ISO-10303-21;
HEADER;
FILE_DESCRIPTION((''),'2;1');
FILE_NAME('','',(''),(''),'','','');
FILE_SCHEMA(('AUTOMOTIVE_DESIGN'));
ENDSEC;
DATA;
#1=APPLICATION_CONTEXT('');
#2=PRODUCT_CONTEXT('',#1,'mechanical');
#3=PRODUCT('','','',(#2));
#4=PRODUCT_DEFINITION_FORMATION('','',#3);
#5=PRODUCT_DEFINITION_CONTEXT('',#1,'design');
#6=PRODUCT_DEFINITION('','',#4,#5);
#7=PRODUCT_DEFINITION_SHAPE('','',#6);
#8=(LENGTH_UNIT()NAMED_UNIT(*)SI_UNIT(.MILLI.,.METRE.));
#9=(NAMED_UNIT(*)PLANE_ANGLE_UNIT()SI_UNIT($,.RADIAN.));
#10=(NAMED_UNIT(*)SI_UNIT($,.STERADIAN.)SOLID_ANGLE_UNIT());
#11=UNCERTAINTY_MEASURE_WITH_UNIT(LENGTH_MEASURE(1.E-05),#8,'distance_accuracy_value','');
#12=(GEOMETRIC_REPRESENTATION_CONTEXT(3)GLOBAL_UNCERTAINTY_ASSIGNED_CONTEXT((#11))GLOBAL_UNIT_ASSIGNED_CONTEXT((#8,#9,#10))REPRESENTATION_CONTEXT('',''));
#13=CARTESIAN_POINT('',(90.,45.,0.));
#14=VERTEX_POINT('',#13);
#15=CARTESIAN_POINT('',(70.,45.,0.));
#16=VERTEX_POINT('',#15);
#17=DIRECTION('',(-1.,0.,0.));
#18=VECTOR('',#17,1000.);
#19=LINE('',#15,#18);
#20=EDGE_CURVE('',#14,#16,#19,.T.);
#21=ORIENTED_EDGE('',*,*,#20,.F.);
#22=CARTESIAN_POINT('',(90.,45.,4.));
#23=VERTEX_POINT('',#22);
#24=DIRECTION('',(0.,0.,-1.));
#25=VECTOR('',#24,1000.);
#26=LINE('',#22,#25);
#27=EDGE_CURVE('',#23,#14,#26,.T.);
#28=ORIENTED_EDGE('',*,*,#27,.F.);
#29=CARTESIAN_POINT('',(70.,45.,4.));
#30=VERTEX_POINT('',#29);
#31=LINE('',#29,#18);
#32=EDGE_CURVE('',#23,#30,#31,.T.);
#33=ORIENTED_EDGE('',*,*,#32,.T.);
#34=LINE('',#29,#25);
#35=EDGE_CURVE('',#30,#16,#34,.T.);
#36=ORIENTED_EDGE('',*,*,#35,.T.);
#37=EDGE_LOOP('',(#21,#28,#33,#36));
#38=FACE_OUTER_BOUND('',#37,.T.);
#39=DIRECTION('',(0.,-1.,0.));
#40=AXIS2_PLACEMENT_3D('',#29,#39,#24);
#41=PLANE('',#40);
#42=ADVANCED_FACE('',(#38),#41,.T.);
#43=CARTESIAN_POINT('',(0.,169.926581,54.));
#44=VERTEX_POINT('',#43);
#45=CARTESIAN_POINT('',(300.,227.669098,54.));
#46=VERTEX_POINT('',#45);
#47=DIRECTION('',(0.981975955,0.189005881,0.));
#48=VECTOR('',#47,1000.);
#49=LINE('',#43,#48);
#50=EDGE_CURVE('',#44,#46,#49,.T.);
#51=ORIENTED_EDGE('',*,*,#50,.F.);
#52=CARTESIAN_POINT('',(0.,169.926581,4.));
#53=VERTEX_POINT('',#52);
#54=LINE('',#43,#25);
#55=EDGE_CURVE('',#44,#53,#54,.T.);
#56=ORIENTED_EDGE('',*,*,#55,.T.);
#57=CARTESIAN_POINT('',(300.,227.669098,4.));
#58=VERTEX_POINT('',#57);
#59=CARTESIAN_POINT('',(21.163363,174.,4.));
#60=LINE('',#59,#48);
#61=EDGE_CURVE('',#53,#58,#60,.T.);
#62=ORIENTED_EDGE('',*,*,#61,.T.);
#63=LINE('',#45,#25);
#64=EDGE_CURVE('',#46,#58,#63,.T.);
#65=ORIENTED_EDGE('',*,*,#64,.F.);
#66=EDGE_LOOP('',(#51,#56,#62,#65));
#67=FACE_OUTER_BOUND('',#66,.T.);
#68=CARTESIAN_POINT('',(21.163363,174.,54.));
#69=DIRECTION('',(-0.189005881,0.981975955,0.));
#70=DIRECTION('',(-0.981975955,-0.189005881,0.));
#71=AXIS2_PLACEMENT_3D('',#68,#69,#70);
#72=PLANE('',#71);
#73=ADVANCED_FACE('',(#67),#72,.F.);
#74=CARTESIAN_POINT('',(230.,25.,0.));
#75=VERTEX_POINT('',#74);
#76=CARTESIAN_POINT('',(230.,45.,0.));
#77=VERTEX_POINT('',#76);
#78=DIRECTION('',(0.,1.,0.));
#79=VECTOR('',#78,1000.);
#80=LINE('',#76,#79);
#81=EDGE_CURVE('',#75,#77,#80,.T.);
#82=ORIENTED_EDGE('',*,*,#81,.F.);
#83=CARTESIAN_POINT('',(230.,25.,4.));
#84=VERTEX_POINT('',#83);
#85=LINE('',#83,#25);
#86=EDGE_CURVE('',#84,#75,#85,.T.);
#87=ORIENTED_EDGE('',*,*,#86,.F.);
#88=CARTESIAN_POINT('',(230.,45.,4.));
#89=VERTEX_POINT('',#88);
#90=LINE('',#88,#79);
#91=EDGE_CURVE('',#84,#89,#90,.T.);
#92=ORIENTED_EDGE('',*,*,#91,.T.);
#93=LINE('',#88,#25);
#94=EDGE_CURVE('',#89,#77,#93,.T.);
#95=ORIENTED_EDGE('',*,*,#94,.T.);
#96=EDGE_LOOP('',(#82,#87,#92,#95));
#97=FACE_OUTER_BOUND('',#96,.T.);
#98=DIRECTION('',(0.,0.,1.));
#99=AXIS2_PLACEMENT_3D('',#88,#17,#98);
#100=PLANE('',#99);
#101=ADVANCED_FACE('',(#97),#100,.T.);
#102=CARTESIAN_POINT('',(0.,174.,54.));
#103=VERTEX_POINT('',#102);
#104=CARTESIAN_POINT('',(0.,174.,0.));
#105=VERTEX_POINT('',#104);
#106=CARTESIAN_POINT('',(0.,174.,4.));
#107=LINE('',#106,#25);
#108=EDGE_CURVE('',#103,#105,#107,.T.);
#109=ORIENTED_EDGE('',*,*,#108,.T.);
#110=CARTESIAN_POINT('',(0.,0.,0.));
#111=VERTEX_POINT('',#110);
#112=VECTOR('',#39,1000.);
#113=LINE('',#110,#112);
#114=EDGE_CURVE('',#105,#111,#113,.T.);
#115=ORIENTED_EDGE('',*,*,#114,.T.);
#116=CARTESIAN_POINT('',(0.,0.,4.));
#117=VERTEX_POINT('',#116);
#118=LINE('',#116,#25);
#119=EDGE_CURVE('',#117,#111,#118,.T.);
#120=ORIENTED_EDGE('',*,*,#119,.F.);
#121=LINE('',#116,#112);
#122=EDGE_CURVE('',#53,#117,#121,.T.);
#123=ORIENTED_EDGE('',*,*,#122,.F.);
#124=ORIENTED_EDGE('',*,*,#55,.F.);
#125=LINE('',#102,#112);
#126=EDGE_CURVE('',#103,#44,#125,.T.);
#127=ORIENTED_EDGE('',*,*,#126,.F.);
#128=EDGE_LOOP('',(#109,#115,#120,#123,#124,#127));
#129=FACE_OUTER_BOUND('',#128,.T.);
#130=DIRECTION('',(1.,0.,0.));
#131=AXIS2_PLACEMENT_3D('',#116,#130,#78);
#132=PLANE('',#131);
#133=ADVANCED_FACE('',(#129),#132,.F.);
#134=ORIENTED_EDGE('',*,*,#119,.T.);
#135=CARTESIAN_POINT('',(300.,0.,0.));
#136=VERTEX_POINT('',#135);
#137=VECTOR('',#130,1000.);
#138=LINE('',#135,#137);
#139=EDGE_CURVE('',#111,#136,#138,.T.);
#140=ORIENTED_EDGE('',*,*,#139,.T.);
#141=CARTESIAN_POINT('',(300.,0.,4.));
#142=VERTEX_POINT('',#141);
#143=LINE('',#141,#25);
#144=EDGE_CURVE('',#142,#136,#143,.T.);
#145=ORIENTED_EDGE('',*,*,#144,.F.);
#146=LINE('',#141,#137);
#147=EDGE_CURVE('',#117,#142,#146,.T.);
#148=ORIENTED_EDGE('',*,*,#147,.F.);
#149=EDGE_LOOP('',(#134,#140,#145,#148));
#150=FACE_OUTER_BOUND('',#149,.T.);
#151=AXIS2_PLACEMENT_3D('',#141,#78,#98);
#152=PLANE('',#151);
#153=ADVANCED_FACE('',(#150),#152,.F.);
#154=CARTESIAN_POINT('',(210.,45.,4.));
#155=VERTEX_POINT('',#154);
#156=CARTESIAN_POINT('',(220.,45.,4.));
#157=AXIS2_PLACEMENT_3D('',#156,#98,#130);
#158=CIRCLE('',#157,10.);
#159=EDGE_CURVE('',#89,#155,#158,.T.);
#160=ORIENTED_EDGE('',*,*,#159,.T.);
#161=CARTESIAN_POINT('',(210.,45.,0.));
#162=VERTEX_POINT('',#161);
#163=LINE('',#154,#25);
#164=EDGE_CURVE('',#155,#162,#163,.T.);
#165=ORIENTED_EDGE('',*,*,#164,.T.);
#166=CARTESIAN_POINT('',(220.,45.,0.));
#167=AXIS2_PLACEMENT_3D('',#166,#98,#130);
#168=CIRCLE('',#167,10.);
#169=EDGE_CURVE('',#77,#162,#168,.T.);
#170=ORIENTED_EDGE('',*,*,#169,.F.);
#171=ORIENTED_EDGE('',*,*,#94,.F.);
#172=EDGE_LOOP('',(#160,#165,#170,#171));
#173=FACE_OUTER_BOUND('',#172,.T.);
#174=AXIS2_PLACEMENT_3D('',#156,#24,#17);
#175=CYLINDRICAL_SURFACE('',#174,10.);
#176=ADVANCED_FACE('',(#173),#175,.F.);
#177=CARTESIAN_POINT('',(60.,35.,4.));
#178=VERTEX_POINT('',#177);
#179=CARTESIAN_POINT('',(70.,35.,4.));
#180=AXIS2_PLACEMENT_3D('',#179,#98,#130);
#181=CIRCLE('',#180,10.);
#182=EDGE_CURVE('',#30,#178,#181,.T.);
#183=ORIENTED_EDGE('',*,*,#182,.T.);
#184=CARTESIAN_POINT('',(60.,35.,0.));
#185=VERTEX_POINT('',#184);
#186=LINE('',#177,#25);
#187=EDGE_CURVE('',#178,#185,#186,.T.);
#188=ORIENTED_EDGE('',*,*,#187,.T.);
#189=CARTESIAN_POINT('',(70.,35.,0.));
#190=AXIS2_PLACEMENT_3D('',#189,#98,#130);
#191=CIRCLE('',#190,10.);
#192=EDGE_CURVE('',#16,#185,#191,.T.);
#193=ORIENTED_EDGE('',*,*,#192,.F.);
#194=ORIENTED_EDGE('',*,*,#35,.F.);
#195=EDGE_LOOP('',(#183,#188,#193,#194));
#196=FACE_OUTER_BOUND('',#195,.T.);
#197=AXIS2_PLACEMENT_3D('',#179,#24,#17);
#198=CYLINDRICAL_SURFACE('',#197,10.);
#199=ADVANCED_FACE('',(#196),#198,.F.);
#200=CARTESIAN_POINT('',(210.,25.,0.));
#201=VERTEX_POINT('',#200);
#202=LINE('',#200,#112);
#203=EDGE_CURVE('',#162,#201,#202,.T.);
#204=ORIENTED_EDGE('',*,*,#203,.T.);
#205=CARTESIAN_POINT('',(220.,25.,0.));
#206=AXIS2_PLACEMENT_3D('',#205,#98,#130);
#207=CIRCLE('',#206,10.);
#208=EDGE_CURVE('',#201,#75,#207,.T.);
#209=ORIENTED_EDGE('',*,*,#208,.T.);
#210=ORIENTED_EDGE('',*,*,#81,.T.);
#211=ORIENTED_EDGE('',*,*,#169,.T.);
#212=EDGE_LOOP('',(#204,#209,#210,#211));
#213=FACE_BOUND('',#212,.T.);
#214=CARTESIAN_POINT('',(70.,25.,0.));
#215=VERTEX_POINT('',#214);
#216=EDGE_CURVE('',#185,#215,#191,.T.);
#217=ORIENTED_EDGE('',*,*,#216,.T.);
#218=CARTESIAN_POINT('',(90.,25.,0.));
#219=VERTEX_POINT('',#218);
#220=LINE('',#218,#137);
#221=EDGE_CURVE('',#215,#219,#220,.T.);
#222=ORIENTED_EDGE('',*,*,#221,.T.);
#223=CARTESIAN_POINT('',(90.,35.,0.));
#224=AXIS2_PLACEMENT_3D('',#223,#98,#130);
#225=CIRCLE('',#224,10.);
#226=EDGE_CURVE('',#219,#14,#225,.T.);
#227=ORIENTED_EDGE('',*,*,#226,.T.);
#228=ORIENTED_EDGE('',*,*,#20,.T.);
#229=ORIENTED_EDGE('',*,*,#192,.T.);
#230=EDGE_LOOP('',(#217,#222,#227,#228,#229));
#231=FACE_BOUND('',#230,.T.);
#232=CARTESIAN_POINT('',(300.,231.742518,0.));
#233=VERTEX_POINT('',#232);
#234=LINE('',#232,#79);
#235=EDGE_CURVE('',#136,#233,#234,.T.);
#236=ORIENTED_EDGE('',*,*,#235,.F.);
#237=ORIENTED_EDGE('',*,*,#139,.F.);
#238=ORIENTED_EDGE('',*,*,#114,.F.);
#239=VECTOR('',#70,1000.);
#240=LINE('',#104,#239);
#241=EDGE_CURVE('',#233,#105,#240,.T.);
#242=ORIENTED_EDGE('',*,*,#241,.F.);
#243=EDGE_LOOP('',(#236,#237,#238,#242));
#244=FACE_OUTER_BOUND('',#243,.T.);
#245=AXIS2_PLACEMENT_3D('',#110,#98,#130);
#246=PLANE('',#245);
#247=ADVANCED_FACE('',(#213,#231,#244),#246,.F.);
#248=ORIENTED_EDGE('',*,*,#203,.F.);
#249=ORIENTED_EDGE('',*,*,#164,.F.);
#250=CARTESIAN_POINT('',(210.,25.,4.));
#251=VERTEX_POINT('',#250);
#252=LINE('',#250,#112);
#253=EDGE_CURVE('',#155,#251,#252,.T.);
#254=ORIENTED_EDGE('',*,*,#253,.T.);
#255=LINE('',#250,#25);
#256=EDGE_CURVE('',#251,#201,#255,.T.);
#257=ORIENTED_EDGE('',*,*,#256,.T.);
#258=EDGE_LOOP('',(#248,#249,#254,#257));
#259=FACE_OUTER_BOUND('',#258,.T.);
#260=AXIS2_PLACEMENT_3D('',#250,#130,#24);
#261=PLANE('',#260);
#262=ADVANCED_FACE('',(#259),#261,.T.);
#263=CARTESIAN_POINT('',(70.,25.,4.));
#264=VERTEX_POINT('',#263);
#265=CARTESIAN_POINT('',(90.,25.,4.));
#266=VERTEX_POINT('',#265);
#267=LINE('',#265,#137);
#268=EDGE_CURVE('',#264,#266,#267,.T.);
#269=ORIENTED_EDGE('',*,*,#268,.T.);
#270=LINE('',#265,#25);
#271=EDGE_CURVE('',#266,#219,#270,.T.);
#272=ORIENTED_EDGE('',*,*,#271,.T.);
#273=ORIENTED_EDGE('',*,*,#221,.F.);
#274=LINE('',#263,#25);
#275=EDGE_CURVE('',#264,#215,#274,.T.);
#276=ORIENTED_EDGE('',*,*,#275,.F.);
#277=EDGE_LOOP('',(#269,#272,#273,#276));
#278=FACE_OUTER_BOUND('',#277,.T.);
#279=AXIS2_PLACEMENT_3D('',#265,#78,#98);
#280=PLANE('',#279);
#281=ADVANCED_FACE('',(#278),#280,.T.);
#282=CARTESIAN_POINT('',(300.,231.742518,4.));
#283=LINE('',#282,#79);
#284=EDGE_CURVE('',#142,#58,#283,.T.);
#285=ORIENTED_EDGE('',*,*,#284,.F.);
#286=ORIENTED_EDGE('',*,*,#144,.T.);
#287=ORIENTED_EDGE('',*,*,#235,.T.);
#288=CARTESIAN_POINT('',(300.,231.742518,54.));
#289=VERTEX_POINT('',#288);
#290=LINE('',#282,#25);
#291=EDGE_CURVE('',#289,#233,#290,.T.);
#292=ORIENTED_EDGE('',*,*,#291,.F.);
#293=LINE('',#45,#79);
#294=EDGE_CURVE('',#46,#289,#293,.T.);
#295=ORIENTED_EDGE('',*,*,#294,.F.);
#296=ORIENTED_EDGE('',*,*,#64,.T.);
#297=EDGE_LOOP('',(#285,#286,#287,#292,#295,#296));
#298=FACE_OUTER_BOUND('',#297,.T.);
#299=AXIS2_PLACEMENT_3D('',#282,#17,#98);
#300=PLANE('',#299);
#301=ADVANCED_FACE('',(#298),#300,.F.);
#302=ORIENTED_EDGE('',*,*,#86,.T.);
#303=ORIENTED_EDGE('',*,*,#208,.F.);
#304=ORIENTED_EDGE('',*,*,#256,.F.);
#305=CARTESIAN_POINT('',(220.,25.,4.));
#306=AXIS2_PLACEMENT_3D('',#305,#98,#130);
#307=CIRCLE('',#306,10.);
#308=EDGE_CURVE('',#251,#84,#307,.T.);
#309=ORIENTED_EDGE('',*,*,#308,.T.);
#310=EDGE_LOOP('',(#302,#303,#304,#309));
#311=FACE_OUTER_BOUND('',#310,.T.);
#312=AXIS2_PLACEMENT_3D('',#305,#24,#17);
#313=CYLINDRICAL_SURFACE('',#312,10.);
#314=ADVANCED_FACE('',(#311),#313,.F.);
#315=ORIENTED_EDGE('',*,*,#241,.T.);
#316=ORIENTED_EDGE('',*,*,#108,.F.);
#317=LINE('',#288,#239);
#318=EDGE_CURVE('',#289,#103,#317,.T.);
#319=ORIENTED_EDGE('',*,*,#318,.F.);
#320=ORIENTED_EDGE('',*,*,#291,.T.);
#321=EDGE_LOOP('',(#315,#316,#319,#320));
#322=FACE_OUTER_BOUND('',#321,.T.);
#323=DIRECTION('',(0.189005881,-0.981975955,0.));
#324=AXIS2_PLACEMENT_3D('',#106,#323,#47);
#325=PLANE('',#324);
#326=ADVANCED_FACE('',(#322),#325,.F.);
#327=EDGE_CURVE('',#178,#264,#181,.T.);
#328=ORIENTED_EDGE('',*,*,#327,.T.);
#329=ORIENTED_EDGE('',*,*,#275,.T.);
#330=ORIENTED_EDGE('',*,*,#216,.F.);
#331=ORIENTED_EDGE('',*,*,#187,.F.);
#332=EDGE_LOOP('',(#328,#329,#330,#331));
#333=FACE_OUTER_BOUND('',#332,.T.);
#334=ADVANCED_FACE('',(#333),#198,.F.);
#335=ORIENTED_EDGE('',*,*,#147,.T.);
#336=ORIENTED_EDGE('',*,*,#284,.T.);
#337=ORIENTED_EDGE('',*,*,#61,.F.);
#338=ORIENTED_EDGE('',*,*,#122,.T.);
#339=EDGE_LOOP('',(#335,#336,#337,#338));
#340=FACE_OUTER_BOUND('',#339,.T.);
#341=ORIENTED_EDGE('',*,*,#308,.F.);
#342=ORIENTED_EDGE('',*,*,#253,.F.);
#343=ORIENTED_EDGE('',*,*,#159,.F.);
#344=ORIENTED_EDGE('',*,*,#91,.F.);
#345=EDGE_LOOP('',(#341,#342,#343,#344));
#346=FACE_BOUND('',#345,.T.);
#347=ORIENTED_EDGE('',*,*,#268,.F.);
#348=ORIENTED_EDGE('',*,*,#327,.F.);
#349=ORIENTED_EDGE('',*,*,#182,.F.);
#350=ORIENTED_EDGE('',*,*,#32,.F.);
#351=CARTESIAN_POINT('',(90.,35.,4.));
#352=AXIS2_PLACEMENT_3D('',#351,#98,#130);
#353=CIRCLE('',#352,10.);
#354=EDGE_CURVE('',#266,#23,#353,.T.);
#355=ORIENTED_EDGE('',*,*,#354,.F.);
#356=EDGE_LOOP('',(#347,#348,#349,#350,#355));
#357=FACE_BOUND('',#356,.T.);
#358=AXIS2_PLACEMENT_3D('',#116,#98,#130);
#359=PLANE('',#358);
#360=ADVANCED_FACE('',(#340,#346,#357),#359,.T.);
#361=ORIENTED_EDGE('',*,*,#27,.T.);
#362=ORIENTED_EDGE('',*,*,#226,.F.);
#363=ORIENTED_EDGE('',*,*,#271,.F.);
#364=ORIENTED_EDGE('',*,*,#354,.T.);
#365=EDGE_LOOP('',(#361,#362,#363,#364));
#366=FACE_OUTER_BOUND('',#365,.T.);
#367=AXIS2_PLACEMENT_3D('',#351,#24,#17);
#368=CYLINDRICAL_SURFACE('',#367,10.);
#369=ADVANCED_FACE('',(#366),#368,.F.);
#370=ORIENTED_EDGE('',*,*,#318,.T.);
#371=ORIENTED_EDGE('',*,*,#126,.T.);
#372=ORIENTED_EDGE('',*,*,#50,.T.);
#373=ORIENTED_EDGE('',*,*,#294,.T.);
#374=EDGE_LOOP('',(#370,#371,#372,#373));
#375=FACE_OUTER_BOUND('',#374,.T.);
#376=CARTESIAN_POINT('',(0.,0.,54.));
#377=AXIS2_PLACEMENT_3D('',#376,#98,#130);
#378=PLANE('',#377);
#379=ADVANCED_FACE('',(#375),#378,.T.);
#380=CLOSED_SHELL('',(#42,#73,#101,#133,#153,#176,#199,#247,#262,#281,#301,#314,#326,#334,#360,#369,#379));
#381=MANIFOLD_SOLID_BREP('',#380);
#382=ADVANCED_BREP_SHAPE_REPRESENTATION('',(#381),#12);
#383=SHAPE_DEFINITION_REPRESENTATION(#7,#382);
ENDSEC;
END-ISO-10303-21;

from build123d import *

# Parameters (mm, degrees)
BOSS_EXTRUDE1_DEPTH = 4
BOSS_EXTRUDE2_DEPTH = 50


with BuildPart() as part:
    # Sketch1 → Boss-Extrude1 (new body)
    with BuildSketch(Plane.XY):
        Polygon((0, 174), (300, 231.742517927), (300, 0), (0, 0), align=None)
        with BuildLine():
            Line((70, 45), (90, 45))
            ThreePointArc((90, 45), (100, 35), (90, 25))
            Line((90, 25), (70, 25))
            ThreePointArc((70, 25), (60, 35), (70, 45))
        make_face(mode=Mode.SUBTRACT)
        with BuildLine():
            Line((230, 45), (230, 25))
            ThreePointArc((230, 25), (220, 15), (210, 25))
            Line((210, 25), (210, 45))
            ThreePointArc((210, 45), (220, 55), (230, 45))
        make_face(mode=Mode.SUBTRACT)
    extrude(amount=BOSS_EXTRUDE1_DEPTH)

    # Sketch2 → Boss-Extrude2 (add)
    with BuildSketch(Plane.XY.offset(4)):
        Polygon((21.16336267, 174), (300, 227.669098433), (300, 231.742517927), (0, 174), (0, 169.926580506), align=None)
    extrude(amount=BOSS_EXTRUDE2_DEPTH)


solid = part.part
